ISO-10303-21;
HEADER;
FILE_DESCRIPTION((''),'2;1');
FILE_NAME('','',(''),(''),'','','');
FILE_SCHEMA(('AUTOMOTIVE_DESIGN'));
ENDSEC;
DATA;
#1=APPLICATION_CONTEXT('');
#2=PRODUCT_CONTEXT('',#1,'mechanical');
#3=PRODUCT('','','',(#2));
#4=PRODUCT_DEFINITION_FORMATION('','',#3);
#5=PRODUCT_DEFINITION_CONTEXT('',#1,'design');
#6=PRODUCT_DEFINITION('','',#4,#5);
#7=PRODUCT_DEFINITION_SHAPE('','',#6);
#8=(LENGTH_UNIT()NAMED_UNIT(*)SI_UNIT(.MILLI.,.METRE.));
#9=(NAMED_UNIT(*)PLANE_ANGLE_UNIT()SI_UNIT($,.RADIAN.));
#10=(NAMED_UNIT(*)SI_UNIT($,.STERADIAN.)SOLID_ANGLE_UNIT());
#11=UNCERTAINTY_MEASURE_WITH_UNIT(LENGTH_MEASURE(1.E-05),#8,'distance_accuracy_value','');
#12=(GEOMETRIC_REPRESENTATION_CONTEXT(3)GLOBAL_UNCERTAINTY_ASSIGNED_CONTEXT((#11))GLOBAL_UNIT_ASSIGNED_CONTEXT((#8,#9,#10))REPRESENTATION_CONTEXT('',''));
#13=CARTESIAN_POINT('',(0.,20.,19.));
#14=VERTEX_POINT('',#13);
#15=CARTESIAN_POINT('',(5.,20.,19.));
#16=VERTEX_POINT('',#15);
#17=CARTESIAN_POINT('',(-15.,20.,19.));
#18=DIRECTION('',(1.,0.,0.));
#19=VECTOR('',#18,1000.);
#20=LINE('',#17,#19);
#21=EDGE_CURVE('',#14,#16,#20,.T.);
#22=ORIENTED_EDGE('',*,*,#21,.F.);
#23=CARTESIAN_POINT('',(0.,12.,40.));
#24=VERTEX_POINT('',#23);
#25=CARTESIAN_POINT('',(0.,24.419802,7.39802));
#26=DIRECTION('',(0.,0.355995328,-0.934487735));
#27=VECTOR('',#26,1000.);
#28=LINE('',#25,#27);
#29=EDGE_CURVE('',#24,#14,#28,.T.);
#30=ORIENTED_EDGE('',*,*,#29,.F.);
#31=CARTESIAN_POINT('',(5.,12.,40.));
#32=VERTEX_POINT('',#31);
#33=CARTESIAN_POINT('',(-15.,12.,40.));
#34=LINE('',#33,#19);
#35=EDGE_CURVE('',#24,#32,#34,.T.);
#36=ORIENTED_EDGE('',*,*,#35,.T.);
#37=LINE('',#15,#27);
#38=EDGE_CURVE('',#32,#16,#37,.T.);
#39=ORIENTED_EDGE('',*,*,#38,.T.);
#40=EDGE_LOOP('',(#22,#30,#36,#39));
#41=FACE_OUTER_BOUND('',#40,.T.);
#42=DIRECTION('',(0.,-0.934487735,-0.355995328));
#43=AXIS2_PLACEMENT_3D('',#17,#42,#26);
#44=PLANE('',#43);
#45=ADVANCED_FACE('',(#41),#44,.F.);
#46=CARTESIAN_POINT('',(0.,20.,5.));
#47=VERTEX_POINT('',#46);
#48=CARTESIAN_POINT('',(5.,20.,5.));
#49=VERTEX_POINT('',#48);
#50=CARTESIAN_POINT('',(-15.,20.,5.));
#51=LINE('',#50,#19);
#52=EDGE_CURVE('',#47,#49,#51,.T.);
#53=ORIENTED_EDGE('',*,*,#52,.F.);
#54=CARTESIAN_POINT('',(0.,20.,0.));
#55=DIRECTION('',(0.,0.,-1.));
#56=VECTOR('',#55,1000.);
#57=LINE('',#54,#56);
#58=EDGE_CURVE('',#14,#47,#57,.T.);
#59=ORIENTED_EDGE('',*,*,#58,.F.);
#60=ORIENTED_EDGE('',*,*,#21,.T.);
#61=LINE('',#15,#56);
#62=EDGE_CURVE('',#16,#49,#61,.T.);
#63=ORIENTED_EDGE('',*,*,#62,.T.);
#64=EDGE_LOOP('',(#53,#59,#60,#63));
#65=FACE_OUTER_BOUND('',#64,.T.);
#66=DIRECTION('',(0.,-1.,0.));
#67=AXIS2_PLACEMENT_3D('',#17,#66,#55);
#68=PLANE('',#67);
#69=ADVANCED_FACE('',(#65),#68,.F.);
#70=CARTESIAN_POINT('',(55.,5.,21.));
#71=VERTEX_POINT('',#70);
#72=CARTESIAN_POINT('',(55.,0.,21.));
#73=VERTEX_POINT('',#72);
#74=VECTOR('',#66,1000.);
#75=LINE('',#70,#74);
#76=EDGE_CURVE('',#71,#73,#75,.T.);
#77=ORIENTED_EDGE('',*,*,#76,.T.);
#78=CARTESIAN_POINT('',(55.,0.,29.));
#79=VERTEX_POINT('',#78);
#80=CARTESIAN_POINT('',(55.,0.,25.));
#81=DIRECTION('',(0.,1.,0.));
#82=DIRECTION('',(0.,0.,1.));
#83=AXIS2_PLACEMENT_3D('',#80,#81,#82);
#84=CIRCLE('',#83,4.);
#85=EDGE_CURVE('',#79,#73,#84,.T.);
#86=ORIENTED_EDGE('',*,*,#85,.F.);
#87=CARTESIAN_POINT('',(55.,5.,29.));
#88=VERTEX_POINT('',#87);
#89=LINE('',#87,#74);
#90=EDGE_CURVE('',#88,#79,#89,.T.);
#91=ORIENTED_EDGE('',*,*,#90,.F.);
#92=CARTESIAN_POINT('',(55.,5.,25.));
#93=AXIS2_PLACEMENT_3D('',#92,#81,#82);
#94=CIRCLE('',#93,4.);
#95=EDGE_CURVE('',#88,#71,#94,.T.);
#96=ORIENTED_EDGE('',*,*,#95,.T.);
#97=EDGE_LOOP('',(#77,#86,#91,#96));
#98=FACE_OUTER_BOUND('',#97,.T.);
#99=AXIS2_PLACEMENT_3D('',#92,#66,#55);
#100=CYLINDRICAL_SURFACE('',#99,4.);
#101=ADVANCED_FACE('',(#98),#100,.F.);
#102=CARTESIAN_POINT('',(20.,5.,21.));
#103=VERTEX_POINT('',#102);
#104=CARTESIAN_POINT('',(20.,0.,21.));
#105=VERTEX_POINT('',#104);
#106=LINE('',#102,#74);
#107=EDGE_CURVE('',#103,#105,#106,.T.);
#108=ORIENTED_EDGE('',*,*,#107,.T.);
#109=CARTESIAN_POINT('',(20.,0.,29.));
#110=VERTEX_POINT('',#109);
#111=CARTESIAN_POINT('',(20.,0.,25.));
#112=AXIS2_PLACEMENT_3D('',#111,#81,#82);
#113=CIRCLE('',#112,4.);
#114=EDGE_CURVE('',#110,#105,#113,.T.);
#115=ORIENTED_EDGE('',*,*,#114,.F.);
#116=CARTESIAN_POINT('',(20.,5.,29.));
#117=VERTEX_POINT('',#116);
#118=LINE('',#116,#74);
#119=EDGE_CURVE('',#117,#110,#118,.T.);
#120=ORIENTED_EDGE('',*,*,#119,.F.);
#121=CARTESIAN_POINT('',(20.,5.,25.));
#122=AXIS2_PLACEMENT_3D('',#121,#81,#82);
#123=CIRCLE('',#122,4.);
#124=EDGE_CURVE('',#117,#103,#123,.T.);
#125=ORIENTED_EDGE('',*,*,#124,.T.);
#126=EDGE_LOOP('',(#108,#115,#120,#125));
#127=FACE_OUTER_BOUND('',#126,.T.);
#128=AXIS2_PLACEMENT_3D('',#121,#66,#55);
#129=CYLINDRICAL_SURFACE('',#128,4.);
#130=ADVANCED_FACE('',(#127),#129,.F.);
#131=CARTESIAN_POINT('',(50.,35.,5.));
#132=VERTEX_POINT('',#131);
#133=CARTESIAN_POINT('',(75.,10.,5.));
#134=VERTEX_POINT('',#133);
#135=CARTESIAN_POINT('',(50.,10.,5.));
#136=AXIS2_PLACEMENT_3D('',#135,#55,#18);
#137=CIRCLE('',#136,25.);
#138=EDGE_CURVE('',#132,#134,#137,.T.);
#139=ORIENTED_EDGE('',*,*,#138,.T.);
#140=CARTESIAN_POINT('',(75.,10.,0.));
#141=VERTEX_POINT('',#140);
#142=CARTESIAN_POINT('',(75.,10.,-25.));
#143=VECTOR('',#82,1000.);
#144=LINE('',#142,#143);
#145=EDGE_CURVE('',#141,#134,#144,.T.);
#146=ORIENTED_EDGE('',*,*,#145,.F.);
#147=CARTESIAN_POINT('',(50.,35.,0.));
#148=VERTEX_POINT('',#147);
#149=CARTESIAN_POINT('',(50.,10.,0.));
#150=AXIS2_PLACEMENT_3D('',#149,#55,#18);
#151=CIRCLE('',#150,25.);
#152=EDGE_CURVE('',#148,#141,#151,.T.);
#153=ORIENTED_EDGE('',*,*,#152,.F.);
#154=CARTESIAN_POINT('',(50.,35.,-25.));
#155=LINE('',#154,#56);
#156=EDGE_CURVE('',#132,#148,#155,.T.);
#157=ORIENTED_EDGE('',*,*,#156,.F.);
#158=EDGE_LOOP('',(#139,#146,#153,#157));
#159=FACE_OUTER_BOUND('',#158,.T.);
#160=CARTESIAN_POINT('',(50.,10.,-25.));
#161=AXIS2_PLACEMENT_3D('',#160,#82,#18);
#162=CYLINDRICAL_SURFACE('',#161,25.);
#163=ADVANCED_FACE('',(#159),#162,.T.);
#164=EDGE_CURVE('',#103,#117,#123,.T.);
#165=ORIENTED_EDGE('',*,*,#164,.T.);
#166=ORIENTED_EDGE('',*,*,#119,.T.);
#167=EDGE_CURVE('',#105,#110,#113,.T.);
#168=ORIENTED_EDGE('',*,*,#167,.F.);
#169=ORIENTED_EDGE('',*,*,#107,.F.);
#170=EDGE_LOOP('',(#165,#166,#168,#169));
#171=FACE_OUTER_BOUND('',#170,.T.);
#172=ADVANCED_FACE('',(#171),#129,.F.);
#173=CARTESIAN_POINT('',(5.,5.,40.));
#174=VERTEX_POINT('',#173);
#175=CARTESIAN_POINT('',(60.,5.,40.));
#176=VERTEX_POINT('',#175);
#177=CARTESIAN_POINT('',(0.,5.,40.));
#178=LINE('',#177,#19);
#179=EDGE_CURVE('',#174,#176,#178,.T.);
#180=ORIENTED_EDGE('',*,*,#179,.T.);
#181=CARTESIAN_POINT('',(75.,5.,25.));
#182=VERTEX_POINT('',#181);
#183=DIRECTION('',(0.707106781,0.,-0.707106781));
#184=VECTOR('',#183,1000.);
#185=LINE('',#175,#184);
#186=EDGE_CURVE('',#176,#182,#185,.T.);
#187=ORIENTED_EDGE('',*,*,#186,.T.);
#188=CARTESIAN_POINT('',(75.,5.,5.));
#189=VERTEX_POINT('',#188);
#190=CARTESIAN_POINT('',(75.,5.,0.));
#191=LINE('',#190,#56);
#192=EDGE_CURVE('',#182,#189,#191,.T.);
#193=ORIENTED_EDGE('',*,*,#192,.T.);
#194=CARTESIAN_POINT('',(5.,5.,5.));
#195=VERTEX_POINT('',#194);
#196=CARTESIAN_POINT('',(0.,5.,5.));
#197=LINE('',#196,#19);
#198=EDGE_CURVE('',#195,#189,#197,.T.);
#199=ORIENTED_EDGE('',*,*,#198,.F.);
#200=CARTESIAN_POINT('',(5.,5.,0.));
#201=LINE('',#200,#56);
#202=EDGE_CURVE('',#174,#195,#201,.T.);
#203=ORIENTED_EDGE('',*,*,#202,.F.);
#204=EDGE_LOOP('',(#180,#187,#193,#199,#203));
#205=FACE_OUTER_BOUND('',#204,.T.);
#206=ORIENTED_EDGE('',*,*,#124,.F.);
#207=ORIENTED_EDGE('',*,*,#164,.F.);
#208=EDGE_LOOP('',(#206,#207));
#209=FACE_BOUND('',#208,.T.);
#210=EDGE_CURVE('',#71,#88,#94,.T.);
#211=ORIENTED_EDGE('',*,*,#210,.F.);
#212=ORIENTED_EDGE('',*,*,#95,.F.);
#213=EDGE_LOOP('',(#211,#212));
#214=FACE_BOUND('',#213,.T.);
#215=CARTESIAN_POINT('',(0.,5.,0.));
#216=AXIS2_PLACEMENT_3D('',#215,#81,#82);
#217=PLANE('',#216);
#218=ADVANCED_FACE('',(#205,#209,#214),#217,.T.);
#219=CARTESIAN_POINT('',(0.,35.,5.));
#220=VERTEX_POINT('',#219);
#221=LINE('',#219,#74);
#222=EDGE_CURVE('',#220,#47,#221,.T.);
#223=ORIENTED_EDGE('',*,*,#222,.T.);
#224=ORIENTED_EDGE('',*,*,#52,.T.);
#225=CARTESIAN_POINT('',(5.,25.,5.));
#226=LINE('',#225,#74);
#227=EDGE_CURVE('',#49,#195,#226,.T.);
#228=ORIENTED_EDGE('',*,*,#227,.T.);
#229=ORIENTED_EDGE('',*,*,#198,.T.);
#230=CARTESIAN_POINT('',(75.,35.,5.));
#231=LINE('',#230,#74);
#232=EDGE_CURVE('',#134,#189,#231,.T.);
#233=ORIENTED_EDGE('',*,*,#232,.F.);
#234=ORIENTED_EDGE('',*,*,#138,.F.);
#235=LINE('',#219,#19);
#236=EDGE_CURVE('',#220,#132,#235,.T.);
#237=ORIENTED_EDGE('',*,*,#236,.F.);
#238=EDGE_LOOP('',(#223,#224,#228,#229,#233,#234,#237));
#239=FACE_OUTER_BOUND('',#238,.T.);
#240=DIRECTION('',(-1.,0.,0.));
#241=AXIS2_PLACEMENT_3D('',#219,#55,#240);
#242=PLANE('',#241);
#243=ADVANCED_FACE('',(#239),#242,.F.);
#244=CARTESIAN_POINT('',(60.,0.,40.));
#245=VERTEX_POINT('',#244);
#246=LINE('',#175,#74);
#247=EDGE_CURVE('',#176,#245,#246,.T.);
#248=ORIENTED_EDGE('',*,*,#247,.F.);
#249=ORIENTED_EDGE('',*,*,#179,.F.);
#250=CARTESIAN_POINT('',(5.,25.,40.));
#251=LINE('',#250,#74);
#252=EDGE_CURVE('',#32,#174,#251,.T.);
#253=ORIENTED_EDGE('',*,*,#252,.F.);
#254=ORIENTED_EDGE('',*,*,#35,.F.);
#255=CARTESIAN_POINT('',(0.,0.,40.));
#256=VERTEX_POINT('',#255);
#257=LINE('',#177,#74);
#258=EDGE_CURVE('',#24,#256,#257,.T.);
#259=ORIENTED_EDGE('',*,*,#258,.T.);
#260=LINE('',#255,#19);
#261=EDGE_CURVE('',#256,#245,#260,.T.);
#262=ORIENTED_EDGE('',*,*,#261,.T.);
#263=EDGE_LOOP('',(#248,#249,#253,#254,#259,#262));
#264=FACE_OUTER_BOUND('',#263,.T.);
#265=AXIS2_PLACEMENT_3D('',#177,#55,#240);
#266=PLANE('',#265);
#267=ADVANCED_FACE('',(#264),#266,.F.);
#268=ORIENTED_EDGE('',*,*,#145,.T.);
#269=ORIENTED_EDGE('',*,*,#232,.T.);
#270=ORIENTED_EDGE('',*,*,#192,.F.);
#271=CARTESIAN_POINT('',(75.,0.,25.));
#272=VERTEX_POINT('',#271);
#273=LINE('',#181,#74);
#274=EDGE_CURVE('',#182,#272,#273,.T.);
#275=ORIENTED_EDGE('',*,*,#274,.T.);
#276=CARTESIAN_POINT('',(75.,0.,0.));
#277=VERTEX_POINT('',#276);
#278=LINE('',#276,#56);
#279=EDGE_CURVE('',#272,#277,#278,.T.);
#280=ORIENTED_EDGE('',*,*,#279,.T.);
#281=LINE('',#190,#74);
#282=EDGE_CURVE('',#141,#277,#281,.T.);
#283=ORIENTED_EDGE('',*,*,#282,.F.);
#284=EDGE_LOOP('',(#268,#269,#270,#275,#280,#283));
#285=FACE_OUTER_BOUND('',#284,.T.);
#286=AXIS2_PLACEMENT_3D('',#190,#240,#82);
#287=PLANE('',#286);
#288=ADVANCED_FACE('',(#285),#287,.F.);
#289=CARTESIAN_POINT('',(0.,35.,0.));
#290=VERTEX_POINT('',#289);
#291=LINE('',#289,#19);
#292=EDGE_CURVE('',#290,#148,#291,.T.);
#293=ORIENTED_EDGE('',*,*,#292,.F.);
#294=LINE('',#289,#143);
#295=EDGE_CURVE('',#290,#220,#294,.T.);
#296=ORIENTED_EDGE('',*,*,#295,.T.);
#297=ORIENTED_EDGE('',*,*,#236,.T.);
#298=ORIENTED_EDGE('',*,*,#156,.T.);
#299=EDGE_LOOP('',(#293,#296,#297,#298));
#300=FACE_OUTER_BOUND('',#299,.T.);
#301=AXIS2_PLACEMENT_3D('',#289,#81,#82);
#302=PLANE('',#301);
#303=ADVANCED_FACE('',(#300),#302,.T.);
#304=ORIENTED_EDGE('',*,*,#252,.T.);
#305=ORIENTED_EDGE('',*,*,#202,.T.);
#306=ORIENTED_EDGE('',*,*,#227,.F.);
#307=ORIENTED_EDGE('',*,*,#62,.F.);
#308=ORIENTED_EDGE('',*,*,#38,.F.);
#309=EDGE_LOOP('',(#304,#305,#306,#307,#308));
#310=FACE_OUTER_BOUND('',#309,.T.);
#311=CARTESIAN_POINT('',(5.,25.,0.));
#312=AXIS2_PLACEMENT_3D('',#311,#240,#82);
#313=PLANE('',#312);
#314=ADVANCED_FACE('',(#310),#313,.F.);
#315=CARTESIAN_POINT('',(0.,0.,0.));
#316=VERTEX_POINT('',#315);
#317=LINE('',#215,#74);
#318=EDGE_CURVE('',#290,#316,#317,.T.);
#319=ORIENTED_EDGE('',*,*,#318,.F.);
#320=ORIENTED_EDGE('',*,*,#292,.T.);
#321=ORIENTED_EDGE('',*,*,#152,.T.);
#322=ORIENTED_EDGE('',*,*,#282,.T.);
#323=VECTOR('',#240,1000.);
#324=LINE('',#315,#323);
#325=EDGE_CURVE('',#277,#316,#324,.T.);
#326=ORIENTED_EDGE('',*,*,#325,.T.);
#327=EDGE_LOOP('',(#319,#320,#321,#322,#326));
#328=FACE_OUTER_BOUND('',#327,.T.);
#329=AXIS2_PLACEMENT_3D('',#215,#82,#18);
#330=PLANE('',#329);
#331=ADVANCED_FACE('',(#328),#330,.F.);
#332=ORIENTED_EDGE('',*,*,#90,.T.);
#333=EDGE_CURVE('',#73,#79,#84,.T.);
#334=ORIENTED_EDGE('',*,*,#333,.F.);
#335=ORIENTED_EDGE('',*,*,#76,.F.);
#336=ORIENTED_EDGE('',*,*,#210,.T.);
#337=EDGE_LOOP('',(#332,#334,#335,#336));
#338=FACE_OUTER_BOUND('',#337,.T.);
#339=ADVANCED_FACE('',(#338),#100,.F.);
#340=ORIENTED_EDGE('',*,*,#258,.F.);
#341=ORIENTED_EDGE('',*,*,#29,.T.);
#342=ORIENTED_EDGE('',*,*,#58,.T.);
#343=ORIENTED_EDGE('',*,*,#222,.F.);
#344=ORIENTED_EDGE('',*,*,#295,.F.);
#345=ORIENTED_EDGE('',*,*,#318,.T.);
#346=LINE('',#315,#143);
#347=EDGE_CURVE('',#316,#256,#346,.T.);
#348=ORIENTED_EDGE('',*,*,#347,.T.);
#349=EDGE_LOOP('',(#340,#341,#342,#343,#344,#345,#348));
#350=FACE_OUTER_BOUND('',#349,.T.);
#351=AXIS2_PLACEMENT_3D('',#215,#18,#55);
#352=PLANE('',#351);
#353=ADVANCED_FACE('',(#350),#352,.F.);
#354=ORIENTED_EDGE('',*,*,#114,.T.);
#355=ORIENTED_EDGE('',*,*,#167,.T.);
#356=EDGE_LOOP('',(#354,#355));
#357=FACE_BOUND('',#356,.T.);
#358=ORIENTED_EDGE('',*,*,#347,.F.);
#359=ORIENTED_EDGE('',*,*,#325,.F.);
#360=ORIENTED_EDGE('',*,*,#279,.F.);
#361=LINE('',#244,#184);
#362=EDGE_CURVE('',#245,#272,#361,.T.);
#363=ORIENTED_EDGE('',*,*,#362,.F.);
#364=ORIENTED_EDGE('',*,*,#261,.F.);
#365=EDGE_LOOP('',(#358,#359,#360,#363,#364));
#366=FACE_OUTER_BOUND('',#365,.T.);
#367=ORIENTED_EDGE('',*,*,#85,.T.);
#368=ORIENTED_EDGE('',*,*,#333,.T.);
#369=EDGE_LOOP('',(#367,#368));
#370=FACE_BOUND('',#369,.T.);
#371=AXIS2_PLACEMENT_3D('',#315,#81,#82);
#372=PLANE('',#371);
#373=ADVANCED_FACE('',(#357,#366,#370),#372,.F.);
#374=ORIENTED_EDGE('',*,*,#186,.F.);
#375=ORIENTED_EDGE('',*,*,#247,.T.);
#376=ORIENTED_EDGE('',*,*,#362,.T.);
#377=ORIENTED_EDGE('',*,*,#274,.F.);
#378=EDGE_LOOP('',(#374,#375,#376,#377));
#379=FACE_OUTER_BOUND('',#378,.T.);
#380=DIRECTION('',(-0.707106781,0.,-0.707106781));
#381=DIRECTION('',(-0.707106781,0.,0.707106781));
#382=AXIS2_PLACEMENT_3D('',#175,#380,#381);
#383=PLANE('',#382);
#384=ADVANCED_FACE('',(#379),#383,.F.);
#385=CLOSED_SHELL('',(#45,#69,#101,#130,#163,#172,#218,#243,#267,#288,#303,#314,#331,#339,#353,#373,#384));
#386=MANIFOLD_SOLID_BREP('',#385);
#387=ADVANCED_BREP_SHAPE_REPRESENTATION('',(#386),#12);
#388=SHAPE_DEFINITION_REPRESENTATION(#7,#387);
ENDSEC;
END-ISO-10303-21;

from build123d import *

# Parameters (mm, degrees)
BASE_PLATE_SKETCH_R           = 4
BASE_PLATE_DEPTH              = 5
SIDE_WALL_SKETCH_W            = 5
SIDE_WALL_SKETCH_H            = 40
SIDE_WALL_DEPTH               = 20
SIDE_WALL_TAPER_CUT_DEPTH     = 20
BACK_WALL_SKETCH_W            = 75
BACK_WALL_SKETCH_H            = 5
BACK_WALL_DEPTH               = 30
BACK_WALL_CORNER_RADIUS_DEPTH = 30


with BuildPart() as part:
    # Base Plate Sketch → Base Plate (new body)
    with BuildSketch(Plane(origin=(0, 0, 0), x_dir=(1, 0, 0), z_dir=(0, 1, 0))):
        Polygon((0, 0), (75, 0), (75, -25), (60, -40), (0, -40), align=None)
        with Locations(Location((20, -25, 0), (0, 0, 270))):
            Circle(BASE_PLATE_SKETCH_R, mode=Mode.SUBTRACT)
        with Locations(Location((55, -25, 0), (0, 0, 270))):
            Circle(BASE_PLATE_SKETCH_R, mode=Mode.SUBTRACT)
    extrude(amount=BASE_PLATE_DEPTH)

    # Side Wall Sketch → Side Wall (add)
    with BuildSketch(Plane(origin=(0, 5, 0), x_dir=(1, 0, 0), z_dir=(0, 1, 0))):
        with Locations((2.5, -20)):
            Rectangle(SIDE_WALL_SKETCH_W, SIDE_WALL_SKETCH_H)
    extrude(amount=SIDE_WALL_DEPTH)

    # Side Wall Taper Sketch → Side Wall Taper Cut (cut)
    with BuildSketch(Plane(origin=(5, 0, 0), x_dir=(0, 0, -1), z_dir=(1, 0, 0))):
        Polygon((-19, 20), (-40, 12), (-40, 25), (0, 25), (0, 20), align=None)
    extrude(amount=-SIDE_WALL_TAPER_CUT_DEPTH, mode=Mode.SUBTRACT)

    # Back Wall Sketch → Back Wall (add)
    with BuildSketch(Plane(origin=(0, 5, 0), x_dir=(1, 0, 0), z_dir=(0, 1, 0))):
        with Locations((37.5, -2.5)):
            Rectangle(BACK_WALL_SKETCH_W, BACK_WALL_SKETCH_H)
    extrude(amount=BACK_WALL_DEPTH)

    # Back Wall Corner Radius Sketch → Back Wall Corner Radius (cut)
    with BuildSketch(Plane.XY.offset(5)):
        with BuildLine():
            Line((50, 35), (75, 35))
            Line((75, 35), (75, 10))
            ThreePointArc((75, 10), (67.67766953, 27.67766953), (50, 35))
        make_face()
    extrude(amount=-BACK_WALL_CORNER_RADIUS_DEPTH, mode=Mode.SUBTRACT)


solid = part.part
